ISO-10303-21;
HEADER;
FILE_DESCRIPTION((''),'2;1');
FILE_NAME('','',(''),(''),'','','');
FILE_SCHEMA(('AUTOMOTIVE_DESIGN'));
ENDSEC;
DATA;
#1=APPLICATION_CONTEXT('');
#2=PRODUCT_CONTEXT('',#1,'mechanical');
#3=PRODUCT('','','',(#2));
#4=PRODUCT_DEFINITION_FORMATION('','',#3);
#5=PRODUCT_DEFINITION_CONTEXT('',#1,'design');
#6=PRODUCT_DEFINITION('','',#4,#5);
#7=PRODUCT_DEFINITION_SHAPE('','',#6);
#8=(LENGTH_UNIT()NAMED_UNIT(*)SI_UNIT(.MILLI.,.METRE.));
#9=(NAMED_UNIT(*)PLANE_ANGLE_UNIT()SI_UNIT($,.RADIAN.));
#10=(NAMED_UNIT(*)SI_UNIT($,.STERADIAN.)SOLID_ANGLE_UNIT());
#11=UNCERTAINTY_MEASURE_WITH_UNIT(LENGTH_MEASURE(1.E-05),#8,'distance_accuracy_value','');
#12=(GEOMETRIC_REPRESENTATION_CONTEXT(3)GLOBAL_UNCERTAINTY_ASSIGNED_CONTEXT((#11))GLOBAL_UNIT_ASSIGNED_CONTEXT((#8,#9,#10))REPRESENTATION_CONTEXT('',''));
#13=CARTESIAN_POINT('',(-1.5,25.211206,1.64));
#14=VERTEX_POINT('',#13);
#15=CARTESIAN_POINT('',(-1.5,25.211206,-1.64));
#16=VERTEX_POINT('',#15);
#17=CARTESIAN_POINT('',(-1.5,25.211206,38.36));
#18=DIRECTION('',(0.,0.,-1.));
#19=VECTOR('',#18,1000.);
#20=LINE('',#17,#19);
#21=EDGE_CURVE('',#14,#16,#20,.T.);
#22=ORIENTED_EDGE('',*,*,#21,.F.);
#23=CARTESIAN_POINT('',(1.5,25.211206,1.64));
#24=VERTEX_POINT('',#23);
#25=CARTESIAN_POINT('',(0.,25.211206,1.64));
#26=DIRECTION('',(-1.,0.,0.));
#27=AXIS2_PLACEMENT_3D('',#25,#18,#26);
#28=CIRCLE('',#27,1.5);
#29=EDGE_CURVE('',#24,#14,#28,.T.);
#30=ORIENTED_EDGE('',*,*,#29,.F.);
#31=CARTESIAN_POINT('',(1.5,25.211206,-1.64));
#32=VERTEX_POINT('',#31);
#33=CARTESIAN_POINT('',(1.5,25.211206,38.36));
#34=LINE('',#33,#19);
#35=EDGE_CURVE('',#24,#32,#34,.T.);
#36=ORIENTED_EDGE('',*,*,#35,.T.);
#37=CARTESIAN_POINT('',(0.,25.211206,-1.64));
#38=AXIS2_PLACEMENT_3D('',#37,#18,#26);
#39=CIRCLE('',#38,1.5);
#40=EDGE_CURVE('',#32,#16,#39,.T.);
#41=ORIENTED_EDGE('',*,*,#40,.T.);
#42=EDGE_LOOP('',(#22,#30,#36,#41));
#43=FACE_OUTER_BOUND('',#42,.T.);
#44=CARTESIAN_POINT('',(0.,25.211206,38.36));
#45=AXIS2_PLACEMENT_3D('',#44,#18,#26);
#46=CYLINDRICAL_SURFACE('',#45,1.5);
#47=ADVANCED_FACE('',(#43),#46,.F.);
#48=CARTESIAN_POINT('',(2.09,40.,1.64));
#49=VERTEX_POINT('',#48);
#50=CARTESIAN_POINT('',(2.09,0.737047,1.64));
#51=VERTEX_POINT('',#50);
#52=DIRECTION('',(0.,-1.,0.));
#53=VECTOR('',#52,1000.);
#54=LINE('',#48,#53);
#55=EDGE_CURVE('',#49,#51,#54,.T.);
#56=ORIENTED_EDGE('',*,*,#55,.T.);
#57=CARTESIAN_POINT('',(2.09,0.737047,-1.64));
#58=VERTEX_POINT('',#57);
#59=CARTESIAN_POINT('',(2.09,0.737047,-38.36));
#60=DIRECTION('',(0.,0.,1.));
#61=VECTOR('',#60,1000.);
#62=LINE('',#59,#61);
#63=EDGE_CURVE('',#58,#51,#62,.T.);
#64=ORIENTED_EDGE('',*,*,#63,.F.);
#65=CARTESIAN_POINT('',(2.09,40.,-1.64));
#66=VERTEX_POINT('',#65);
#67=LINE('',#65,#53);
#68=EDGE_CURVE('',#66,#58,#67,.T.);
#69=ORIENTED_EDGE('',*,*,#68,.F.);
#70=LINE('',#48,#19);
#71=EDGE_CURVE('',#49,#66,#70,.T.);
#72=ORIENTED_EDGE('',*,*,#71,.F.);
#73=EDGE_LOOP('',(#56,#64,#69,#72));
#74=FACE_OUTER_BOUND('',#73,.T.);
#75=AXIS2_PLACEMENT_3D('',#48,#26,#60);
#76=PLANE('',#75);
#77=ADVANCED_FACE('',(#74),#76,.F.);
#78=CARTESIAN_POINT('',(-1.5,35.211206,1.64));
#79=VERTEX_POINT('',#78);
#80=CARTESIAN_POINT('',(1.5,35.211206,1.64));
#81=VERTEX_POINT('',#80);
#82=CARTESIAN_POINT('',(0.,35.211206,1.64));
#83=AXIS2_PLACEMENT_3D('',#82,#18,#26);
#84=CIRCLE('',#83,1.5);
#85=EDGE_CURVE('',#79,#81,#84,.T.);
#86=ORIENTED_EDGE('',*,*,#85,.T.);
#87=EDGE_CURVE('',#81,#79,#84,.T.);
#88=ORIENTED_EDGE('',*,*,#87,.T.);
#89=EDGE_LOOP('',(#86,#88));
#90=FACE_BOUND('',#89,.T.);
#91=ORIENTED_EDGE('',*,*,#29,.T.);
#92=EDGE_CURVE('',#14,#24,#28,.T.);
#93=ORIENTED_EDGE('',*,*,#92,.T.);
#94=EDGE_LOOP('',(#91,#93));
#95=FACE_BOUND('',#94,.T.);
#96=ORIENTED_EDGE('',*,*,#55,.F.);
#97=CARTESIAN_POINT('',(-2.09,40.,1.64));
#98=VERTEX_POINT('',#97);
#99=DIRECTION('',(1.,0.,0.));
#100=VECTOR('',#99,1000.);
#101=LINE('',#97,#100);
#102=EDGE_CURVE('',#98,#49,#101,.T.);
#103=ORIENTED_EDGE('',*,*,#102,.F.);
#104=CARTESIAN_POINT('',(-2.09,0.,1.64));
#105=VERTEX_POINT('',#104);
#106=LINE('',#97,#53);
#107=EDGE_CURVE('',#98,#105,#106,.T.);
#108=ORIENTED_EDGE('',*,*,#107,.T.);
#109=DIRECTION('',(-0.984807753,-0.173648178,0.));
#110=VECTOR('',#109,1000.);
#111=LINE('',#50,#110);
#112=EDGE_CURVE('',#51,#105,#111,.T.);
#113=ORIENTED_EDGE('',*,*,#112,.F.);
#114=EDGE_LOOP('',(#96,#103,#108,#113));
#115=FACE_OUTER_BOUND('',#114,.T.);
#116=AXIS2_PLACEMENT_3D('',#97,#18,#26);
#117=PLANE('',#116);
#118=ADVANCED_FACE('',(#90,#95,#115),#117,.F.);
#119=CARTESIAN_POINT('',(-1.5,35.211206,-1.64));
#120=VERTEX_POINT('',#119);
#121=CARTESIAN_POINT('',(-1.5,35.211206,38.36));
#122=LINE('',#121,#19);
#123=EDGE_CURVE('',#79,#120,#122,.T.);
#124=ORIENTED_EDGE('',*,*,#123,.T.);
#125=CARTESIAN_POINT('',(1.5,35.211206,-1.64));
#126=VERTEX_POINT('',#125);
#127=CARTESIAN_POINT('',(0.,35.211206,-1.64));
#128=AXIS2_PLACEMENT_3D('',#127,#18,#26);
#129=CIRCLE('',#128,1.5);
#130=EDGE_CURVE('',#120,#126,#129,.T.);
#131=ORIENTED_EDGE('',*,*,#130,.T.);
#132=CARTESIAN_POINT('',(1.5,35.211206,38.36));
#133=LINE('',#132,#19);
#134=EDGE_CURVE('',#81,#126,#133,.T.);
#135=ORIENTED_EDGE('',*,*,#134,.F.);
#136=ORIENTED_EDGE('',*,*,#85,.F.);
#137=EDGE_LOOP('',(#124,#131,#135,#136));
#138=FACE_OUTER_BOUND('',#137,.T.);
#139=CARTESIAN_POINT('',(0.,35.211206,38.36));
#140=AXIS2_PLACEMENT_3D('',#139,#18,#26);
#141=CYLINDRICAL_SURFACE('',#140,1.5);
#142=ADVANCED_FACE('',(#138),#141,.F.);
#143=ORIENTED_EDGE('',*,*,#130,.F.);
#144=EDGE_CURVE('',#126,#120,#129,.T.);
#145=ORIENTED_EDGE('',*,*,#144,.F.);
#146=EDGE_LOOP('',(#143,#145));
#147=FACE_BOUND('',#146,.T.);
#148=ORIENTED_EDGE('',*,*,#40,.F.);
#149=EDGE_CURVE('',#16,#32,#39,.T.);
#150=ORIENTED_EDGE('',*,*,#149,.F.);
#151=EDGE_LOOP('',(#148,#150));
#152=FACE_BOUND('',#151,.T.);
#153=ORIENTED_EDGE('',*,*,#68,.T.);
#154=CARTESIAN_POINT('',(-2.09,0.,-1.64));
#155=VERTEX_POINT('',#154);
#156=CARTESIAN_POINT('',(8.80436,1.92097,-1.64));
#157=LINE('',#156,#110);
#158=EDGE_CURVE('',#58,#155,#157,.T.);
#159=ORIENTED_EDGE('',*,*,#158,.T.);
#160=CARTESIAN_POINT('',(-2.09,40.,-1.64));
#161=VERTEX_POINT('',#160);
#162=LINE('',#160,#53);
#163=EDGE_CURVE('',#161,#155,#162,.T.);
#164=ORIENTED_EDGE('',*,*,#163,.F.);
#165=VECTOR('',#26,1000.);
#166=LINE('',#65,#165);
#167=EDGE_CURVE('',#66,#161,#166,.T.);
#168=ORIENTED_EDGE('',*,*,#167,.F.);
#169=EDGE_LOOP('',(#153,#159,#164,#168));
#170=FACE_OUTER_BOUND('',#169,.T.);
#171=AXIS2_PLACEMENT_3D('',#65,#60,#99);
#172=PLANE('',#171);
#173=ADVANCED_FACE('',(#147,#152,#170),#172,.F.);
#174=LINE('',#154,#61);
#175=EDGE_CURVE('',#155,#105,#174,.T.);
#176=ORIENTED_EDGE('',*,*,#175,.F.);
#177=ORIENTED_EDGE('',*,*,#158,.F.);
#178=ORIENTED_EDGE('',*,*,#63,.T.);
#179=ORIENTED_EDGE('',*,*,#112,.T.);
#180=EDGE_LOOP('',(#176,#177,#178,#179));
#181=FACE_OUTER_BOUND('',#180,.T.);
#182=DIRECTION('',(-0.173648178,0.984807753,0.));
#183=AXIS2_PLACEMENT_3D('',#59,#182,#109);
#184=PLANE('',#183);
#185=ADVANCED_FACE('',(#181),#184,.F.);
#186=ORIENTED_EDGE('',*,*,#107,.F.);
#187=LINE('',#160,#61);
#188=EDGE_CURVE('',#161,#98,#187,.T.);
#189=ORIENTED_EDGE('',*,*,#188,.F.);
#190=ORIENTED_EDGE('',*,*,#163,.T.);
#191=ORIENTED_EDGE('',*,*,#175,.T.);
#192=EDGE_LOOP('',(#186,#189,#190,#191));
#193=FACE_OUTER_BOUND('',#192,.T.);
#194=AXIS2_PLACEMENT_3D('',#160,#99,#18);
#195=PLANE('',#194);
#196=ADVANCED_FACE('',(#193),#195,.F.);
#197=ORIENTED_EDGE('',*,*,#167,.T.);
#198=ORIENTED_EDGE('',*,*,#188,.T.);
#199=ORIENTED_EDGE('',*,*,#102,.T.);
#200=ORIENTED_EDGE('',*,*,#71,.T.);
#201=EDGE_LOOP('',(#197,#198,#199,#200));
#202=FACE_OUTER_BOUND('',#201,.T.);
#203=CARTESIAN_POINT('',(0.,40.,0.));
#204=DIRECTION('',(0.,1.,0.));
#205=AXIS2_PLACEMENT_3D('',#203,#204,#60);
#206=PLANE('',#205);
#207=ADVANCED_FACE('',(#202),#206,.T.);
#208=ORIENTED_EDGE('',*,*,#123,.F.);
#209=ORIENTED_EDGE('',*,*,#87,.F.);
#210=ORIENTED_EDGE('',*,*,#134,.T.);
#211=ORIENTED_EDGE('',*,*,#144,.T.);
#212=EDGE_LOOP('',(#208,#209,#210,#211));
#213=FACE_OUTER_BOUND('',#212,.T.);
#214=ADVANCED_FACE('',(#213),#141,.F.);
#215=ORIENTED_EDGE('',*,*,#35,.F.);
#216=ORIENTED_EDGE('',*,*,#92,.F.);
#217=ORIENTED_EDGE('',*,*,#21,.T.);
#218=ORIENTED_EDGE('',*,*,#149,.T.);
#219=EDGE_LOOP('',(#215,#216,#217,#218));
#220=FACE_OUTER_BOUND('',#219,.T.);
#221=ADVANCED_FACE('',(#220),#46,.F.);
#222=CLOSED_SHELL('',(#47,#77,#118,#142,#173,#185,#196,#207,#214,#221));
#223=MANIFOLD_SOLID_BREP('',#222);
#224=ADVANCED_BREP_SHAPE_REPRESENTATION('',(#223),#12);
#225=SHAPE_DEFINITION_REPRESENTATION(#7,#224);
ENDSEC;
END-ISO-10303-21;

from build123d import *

# Parameters (mm, degrees)
SKETCH1_W           = 4.18
SKETCH1_H           = 3.28
BOSS_EXTRUDE1_DEPTH = 40
CUT_EXTRUDE1_DEPTH  = 40
SKETCH3_R           = 1.5
CUT_EXTRUDE2_DEPTH  = 40


with BuildPart() as part:
    # Sketch1 → Boss-Extrude1 (new body)
    with BuildSketch(Plane(origin=(0, 0, 0), x_dir=(1, 0, 0), z_dir=(0, 1, 0))):
        Rectangle(SKETCH1_W, SKETCH1_H)
    extrude(amount=BOSS_EXTRUDE1_DEPTH)

    # Sketch2 → Cut-Extrude1 (cut)
    with BuildSketch(Plane.XY.offset(1.64)):
        Polygon((-2.09, 0), (2.09, 0), (2.09, 0.737046779), align=None)
    extrude(amount=-CUT_EXTRUDE1_DEPTH, mode=Mode.SUBTRACT)

    # Sketch3 → Cut-Extrude2 (cut)
    with BuildSketch(Plane(origin=(0, 0, -1.64), x_dir=(-1, 0, 0), z_dir=(0, 0, -1))):
        with Locations((0, 35.211206118)):
            Circle(SKETCH3_R)
        with Locations((0, 25.211206118)):
            Circle(SKETCH3_R)
    extrude(amount=-CUT_EXTRUDE2_DEPTH, mode=Mode.SUBTRACT)


solid = part.part
